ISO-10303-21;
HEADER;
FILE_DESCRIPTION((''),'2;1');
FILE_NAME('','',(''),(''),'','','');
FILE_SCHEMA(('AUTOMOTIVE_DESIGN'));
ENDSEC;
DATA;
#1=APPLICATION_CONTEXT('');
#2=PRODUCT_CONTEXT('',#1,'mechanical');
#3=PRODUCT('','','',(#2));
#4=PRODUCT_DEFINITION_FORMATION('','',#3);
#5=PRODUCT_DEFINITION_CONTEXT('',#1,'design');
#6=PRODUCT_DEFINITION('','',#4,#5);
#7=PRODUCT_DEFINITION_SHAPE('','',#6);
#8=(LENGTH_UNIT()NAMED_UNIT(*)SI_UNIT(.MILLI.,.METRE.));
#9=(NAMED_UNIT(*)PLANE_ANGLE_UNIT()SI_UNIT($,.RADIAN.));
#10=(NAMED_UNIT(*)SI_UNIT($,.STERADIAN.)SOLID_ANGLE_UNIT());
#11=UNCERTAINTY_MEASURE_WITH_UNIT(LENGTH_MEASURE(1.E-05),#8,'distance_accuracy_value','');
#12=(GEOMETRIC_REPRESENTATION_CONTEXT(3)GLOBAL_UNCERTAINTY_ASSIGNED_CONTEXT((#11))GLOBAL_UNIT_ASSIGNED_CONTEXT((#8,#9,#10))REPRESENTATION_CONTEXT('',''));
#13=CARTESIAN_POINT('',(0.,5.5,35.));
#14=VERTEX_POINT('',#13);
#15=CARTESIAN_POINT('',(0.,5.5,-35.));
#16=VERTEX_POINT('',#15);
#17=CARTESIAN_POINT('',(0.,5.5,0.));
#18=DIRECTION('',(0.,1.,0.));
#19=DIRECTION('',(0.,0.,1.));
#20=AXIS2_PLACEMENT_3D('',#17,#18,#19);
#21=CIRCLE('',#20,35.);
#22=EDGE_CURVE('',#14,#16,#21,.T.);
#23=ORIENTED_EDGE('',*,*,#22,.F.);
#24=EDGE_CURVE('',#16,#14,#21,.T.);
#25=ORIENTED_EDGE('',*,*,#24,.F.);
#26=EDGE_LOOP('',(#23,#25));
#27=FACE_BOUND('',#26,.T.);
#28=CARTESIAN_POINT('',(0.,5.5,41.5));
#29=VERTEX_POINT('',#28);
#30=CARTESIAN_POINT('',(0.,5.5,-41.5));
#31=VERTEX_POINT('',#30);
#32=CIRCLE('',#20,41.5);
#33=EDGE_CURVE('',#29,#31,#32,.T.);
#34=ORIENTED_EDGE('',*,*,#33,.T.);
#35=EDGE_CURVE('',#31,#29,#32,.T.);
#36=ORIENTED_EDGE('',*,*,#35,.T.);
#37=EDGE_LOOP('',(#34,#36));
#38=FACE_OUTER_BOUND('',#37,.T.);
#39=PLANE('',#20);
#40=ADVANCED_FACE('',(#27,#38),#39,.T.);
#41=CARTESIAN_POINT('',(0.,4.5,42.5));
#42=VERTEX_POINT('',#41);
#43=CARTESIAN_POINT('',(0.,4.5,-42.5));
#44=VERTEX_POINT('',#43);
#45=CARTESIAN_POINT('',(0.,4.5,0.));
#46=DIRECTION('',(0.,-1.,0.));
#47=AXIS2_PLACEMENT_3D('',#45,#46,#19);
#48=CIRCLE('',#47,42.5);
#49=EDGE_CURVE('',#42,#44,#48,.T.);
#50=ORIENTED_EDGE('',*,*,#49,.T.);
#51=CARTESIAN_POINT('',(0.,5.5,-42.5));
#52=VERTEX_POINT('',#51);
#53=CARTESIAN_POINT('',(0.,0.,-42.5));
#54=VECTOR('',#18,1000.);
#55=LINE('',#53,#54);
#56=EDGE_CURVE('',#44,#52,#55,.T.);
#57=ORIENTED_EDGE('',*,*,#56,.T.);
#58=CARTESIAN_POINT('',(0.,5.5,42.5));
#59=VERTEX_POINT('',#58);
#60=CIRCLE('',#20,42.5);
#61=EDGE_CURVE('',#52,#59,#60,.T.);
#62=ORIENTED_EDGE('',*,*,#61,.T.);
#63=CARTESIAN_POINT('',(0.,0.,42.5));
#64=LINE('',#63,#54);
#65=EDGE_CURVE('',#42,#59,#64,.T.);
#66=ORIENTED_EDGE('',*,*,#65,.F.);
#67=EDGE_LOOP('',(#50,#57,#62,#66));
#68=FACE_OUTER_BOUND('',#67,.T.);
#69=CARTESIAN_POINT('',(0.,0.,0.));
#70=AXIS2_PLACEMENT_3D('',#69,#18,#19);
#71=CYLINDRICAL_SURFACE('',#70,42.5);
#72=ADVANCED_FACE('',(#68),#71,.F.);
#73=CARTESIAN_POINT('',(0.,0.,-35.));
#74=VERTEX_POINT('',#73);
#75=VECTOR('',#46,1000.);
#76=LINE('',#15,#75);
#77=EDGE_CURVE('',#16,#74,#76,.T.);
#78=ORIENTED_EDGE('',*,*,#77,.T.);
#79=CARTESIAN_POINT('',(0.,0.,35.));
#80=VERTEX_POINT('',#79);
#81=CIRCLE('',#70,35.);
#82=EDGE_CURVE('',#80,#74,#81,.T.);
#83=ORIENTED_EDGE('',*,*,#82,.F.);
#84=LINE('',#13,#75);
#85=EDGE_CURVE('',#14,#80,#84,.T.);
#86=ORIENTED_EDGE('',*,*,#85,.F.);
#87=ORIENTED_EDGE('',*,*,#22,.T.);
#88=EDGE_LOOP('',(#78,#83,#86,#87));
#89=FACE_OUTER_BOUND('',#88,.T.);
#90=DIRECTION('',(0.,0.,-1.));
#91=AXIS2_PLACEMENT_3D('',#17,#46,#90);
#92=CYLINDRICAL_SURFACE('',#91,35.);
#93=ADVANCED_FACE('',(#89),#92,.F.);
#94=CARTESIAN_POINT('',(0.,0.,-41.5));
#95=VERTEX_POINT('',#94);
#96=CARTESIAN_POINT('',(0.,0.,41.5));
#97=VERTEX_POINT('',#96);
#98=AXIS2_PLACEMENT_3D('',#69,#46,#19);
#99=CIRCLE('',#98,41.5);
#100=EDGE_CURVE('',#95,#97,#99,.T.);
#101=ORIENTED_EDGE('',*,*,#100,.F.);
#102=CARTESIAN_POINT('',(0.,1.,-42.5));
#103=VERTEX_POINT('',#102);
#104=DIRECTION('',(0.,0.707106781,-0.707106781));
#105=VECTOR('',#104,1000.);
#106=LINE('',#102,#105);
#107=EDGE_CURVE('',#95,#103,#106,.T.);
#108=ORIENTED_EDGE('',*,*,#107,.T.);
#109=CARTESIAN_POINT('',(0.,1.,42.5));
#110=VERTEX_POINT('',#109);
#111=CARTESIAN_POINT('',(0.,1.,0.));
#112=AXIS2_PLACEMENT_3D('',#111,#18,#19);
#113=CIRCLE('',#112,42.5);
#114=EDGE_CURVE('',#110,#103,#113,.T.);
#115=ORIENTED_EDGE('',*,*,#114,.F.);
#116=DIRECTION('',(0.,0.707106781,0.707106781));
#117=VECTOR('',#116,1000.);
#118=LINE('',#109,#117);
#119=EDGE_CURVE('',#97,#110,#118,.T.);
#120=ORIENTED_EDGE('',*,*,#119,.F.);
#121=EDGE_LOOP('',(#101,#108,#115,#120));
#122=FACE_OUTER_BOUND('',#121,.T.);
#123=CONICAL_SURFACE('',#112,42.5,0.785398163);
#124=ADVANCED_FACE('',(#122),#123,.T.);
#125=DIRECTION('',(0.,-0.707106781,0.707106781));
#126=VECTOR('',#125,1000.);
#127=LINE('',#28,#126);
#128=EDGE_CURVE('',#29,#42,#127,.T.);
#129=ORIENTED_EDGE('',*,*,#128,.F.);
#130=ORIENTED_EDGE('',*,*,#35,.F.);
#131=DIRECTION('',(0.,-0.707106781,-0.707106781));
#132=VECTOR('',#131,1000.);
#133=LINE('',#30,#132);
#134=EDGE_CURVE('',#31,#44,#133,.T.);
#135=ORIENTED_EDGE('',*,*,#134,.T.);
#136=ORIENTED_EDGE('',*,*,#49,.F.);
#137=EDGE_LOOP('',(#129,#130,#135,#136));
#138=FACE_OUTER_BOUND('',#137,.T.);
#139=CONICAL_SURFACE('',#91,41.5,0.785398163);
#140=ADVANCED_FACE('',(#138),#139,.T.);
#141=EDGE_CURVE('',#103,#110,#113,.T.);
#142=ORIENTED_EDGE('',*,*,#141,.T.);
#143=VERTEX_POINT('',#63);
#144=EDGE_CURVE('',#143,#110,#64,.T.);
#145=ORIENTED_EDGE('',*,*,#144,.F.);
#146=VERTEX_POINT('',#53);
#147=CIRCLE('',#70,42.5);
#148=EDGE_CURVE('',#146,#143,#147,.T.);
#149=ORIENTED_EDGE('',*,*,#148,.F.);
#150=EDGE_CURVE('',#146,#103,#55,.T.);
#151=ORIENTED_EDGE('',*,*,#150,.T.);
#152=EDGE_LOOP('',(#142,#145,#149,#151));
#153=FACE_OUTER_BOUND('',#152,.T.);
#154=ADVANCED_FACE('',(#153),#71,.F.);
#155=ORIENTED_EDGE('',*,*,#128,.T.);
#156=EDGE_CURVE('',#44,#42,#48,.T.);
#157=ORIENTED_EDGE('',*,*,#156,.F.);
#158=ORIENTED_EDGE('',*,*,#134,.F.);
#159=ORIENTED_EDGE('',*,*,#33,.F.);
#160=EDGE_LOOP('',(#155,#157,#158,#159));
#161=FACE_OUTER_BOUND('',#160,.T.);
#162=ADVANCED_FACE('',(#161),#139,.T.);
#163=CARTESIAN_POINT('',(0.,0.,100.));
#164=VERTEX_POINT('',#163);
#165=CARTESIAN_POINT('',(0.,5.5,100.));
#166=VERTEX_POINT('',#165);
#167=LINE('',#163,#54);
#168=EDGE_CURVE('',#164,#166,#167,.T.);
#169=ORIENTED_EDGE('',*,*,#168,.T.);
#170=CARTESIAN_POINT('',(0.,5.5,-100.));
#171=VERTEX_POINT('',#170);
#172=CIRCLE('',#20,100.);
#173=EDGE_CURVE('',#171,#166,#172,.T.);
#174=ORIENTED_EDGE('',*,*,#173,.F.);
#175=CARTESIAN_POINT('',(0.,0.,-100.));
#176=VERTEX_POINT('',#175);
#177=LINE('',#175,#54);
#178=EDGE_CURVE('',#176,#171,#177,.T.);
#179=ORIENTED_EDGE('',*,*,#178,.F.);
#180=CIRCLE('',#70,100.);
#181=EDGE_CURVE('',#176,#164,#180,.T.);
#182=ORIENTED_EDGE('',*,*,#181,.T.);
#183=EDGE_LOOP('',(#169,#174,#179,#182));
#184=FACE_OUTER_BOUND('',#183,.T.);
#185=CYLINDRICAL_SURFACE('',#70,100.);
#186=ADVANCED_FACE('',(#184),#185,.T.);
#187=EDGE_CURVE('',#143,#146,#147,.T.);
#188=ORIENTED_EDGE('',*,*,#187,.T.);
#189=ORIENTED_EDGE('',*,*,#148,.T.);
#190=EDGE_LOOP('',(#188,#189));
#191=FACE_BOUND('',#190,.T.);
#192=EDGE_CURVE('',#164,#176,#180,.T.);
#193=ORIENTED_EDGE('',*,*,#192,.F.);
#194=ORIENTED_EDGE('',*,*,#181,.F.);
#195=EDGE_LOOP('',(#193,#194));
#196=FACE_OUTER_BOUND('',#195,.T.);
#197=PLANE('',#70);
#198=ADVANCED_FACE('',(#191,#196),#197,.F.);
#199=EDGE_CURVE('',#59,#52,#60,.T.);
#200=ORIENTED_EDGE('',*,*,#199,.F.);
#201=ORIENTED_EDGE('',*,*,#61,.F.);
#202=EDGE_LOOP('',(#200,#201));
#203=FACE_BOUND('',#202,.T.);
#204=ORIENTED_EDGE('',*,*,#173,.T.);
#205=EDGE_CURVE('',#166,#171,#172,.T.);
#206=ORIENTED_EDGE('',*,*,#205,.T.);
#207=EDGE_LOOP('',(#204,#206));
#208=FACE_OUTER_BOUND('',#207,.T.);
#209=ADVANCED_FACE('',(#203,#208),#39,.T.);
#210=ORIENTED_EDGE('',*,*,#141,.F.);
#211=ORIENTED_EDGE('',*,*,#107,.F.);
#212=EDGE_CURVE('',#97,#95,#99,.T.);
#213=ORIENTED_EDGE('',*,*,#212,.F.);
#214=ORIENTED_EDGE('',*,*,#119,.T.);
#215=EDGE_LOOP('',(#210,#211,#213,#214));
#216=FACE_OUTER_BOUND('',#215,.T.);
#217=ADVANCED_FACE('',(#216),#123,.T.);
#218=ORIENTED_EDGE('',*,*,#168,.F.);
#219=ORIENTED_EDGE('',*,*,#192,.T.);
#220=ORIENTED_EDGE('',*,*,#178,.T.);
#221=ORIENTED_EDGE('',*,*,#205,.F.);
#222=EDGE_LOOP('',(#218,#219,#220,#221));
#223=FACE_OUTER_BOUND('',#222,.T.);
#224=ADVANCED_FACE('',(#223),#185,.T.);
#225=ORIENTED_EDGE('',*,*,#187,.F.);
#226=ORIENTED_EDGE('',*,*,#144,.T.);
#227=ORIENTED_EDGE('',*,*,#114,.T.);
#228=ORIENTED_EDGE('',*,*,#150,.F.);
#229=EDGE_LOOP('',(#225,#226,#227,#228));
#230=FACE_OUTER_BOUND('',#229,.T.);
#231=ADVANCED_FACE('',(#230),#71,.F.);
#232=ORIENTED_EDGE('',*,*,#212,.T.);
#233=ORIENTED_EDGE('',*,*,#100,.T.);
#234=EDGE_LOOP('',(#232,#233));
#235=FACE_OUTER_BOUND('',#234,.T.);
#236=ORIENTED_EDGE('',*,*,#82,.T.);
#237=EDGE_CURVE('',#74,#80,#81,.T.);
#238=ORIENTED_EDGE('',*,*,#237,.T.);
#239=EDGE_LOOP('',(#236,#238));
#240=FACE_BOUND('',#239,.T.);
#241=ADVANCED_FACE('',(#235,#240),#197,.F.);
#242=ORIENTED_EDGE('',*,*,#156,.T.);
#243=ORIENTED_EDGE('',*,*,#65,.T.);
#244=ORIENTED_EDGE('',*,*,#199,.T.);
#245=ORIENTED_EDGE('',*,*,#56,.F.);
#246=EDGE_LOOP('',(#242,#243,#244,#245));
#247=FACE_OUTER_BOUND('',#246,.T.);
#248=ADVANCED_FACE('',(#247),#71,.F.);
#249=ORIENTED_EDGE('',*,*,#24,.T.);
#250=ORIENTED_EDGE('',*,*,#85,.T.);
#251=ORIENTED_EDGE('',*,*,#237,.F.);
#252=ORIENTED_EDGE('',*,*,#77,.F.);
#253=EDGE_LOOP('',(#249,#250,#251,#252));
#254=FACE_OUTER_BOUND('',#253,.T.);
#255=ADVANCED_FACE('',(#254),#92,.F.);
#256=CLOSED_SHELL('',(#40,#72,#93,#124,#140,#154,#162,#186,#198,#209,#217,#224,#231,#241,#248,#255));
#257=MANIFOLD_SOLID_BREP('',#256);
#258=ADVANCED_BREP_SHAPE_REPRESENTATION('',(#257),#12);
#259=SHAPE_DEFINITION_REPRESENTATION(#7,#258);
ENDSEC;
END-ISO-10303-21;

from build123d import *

# Parameters (mm, degrees)
SKETCH1_R           = 42.5
SKETCH1_R_2         = 35
BOSS_EXTRUDE1_DEPTH = 5.5
CHAMFER1_SIZE       = 1
BOSS_EXTRUDE2_START = -5.5
SKETCH2_R           = 100
SKETCH2_R_2         = 42.5
BOSS_EXTRUDE2_DEPTH = 5.5


with BuildPart() as part:
    # Sketch1 → Boss-Extrude1 (new body)
    with BuildSketch(Plane(origin=(0, 0, 0), x_dir=(1, 0, 0), z_dir=(0, 1, 0))):
        with Locations(Location((0, 0, 0), (0, 0, 270))):
            Circle(SKETCH1_R)
        with Locations(Location((0, 0, 0), (0, 0, 270))):
            Circle(SKETCH1_R_2, mode=Mode.SUBTRACT)
    extrude(amount=BOSS_EXTRUDE1_DEPTH)

    # Chamfer1
    chamfer1_edges = [part.edges().sort_by_distance(p)[0] for p in [
        (0, 0, -42.5),
        (0, 5.5, -42.5),
    ]]
    chamfer(chamfer1_edges, length=CHAMFER1_SIZE)

    # Sketch2 → Boss-Extrude2 (add)
    with BuildSketch(Plane(origin=(0, 5.5, 0), x_dir=(1, 0, 0), z_dir=(0, 1, 0)).offset(BOSS_EXTRUDE2_START)):
        with Locations(Location((0, 0, 0), (0, 0, 270))):
            Circle(SKETCH2_R)
        with Locations(Location((0, 0, 0), (0, 0, 270))):
            Circle(SKETCH2_R_2, mode=Mode.SUBTRACT)
    extrude(amount=BOSS_EXTRUDE2_DEPTH)


solid = part.part
